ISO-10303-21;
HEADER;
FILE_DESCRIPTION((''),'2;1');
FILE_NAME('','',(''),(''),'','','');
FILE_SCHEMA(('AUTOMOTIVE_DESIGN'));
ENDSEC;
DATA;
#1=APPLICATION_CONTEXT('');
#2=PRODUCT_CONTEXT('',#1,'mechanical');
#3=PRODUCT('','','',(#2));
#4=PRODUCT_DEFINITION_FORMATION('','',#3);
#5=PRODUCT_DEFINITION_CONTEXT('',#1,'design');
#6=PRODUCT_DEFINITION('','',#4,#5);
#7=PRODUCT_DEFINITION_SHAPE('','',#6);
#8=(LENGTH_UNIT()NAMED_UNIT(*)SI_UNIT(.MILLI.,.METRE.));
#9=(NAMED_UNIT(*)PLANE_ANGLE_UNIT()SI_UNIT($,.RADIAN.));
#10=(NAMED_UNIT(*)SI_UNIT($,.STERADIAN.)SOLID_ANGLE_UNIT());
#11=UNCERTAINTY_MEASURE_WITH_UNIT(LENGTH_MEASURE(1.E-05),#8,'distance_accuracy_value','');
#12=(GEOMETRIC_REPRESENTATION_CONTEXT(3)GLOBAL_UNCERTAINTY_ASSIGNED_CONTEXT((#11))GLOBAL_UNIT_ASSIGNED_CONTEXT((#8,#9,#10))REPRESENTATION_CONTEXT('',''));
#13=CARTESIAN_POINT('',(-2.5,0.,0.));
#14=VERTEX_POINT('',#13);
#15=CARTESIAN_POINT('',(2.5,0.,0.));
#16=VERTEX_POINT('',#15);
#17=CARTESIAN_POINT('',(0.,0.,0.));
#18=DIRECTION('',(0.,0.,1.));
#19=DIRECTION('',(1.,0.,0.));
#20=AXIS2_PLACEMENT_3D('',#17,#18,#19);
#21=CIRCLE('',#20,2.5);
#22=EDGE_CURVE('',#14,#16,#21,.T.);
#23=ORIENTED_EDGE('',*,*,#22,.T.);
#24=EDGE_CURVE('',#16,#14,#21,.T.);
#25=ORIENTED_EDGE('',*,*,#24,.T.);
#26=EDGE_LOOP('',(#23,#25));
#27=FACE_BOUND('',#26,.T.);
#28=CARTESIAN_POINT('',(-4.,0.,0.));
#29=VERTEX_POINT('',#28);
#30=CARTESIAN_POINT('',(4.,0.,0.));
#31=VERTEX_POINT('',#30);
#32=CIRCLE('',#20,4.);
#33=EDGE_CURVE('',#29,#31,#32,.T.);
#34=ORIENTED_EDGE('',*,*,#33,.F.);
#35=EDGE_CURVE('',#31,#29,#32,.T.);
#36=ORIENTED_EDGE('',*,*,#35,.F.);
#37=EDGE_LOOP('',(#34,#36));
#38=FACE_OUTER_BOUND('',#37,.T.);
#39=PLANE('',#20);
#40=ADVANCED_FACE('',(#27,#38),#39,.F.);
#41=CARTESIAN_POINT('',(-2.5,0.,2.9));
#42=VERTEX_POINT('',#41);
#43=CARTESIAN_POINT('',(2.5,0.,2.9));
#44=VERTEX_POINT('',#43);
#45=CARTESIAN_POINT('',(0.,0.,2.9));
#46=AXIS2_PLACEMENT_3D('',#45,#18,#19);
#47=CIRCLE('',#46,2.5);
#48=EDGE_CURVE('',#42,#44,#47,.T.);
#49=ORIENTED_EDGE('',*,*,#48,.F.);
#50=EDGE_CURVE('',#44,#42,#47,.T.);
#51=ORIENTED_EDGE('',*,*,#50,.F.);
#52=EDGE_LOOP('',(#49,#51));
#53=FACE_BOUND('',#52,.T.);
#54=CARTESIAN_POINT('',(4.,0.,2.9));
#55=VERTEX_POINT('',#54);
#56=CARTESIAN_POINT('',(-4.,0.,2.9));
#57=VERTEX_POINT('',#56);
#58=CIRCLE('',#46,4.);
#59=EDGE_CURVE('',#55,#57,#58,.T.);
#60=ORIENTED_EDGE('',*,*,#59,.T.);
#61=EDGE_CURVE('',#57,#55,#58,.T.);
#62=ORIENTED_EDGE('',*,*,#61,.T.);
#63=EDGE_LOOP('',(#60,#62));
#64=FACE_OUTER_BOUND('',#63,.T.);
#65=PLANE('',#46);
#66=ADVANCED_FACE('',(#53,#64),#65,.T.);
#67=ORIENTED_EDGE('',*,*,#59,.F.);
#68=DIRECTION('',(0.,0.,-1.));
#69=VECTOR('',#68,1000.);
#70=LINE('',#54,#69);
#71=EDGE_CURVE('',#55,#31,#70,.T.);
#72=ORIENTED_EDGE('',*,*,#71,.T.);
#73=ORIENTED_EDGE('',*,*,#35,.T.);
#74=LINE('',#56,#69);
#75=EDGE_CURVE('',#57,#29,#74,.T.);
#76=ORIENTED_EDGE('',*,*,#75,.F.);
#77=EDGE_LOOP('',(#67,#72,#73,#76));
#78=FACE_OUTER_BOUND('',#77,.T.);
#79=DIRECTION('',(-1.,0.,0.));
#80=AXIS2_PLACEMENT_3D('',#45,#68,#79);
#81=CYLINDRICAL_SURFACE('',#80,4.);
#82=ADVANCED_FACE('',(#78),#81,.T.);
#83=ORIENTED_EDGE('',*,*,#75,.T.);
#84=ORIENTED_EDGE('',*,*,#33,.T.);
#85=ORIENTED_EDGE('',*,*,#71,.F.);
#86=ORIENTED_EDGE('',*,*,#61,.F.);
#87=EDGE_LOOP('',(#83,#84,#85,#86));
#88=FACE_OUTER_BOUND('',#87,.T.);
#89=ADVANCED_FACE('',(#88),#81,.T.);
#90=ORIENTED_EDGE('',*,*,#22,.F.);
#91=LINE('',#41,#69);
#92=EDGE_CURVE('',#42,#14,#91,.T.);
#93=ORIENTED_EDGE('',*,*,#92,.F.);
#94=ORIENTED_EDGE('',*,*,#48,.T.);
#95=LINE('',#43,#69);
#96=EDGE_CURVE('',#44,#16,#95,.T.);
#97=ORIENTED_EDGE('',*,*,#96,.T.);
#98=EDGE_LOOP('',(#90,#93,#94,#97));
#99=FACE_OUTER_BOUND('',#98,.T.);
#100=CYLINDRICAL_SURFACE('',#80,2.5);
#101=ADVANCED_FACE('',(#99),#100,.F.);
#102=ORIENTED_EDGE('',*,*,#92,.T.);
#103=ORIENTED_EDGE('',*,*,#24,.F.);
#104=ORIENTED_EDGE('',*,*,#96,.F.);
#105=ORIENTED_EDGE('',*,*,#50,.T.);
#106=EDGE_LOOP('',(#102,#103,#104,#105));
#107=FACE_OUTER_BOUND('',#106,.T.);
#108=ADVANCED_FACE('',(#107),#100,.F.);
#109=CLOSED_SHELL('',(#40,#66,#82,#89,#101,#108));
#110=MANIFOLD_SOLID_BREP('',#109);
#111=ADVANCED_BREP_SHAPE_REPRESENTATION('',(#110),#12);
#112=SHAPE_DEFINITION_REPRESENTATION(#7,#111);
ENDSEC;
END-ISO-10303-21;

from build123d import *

# Parameters (mm, degrees)
SKETCH1_R           = 4
SKETCH1_R_2         = 2.5
BOSS_EXTRUDE1_DEPTH = 2.9


with BuildPart() as part:
    # Sketch1 → Boss-Extrude1 (new body)
    with BuildSketch(Plane.XY):
        Circle(SKETCH1_R)
        Circle(SKETCH1_R_2, mode=Mode.SUBTRACT)
    extrude(amount=BOSS_EXTRUDE1_DEPTH)


solid = part.part
